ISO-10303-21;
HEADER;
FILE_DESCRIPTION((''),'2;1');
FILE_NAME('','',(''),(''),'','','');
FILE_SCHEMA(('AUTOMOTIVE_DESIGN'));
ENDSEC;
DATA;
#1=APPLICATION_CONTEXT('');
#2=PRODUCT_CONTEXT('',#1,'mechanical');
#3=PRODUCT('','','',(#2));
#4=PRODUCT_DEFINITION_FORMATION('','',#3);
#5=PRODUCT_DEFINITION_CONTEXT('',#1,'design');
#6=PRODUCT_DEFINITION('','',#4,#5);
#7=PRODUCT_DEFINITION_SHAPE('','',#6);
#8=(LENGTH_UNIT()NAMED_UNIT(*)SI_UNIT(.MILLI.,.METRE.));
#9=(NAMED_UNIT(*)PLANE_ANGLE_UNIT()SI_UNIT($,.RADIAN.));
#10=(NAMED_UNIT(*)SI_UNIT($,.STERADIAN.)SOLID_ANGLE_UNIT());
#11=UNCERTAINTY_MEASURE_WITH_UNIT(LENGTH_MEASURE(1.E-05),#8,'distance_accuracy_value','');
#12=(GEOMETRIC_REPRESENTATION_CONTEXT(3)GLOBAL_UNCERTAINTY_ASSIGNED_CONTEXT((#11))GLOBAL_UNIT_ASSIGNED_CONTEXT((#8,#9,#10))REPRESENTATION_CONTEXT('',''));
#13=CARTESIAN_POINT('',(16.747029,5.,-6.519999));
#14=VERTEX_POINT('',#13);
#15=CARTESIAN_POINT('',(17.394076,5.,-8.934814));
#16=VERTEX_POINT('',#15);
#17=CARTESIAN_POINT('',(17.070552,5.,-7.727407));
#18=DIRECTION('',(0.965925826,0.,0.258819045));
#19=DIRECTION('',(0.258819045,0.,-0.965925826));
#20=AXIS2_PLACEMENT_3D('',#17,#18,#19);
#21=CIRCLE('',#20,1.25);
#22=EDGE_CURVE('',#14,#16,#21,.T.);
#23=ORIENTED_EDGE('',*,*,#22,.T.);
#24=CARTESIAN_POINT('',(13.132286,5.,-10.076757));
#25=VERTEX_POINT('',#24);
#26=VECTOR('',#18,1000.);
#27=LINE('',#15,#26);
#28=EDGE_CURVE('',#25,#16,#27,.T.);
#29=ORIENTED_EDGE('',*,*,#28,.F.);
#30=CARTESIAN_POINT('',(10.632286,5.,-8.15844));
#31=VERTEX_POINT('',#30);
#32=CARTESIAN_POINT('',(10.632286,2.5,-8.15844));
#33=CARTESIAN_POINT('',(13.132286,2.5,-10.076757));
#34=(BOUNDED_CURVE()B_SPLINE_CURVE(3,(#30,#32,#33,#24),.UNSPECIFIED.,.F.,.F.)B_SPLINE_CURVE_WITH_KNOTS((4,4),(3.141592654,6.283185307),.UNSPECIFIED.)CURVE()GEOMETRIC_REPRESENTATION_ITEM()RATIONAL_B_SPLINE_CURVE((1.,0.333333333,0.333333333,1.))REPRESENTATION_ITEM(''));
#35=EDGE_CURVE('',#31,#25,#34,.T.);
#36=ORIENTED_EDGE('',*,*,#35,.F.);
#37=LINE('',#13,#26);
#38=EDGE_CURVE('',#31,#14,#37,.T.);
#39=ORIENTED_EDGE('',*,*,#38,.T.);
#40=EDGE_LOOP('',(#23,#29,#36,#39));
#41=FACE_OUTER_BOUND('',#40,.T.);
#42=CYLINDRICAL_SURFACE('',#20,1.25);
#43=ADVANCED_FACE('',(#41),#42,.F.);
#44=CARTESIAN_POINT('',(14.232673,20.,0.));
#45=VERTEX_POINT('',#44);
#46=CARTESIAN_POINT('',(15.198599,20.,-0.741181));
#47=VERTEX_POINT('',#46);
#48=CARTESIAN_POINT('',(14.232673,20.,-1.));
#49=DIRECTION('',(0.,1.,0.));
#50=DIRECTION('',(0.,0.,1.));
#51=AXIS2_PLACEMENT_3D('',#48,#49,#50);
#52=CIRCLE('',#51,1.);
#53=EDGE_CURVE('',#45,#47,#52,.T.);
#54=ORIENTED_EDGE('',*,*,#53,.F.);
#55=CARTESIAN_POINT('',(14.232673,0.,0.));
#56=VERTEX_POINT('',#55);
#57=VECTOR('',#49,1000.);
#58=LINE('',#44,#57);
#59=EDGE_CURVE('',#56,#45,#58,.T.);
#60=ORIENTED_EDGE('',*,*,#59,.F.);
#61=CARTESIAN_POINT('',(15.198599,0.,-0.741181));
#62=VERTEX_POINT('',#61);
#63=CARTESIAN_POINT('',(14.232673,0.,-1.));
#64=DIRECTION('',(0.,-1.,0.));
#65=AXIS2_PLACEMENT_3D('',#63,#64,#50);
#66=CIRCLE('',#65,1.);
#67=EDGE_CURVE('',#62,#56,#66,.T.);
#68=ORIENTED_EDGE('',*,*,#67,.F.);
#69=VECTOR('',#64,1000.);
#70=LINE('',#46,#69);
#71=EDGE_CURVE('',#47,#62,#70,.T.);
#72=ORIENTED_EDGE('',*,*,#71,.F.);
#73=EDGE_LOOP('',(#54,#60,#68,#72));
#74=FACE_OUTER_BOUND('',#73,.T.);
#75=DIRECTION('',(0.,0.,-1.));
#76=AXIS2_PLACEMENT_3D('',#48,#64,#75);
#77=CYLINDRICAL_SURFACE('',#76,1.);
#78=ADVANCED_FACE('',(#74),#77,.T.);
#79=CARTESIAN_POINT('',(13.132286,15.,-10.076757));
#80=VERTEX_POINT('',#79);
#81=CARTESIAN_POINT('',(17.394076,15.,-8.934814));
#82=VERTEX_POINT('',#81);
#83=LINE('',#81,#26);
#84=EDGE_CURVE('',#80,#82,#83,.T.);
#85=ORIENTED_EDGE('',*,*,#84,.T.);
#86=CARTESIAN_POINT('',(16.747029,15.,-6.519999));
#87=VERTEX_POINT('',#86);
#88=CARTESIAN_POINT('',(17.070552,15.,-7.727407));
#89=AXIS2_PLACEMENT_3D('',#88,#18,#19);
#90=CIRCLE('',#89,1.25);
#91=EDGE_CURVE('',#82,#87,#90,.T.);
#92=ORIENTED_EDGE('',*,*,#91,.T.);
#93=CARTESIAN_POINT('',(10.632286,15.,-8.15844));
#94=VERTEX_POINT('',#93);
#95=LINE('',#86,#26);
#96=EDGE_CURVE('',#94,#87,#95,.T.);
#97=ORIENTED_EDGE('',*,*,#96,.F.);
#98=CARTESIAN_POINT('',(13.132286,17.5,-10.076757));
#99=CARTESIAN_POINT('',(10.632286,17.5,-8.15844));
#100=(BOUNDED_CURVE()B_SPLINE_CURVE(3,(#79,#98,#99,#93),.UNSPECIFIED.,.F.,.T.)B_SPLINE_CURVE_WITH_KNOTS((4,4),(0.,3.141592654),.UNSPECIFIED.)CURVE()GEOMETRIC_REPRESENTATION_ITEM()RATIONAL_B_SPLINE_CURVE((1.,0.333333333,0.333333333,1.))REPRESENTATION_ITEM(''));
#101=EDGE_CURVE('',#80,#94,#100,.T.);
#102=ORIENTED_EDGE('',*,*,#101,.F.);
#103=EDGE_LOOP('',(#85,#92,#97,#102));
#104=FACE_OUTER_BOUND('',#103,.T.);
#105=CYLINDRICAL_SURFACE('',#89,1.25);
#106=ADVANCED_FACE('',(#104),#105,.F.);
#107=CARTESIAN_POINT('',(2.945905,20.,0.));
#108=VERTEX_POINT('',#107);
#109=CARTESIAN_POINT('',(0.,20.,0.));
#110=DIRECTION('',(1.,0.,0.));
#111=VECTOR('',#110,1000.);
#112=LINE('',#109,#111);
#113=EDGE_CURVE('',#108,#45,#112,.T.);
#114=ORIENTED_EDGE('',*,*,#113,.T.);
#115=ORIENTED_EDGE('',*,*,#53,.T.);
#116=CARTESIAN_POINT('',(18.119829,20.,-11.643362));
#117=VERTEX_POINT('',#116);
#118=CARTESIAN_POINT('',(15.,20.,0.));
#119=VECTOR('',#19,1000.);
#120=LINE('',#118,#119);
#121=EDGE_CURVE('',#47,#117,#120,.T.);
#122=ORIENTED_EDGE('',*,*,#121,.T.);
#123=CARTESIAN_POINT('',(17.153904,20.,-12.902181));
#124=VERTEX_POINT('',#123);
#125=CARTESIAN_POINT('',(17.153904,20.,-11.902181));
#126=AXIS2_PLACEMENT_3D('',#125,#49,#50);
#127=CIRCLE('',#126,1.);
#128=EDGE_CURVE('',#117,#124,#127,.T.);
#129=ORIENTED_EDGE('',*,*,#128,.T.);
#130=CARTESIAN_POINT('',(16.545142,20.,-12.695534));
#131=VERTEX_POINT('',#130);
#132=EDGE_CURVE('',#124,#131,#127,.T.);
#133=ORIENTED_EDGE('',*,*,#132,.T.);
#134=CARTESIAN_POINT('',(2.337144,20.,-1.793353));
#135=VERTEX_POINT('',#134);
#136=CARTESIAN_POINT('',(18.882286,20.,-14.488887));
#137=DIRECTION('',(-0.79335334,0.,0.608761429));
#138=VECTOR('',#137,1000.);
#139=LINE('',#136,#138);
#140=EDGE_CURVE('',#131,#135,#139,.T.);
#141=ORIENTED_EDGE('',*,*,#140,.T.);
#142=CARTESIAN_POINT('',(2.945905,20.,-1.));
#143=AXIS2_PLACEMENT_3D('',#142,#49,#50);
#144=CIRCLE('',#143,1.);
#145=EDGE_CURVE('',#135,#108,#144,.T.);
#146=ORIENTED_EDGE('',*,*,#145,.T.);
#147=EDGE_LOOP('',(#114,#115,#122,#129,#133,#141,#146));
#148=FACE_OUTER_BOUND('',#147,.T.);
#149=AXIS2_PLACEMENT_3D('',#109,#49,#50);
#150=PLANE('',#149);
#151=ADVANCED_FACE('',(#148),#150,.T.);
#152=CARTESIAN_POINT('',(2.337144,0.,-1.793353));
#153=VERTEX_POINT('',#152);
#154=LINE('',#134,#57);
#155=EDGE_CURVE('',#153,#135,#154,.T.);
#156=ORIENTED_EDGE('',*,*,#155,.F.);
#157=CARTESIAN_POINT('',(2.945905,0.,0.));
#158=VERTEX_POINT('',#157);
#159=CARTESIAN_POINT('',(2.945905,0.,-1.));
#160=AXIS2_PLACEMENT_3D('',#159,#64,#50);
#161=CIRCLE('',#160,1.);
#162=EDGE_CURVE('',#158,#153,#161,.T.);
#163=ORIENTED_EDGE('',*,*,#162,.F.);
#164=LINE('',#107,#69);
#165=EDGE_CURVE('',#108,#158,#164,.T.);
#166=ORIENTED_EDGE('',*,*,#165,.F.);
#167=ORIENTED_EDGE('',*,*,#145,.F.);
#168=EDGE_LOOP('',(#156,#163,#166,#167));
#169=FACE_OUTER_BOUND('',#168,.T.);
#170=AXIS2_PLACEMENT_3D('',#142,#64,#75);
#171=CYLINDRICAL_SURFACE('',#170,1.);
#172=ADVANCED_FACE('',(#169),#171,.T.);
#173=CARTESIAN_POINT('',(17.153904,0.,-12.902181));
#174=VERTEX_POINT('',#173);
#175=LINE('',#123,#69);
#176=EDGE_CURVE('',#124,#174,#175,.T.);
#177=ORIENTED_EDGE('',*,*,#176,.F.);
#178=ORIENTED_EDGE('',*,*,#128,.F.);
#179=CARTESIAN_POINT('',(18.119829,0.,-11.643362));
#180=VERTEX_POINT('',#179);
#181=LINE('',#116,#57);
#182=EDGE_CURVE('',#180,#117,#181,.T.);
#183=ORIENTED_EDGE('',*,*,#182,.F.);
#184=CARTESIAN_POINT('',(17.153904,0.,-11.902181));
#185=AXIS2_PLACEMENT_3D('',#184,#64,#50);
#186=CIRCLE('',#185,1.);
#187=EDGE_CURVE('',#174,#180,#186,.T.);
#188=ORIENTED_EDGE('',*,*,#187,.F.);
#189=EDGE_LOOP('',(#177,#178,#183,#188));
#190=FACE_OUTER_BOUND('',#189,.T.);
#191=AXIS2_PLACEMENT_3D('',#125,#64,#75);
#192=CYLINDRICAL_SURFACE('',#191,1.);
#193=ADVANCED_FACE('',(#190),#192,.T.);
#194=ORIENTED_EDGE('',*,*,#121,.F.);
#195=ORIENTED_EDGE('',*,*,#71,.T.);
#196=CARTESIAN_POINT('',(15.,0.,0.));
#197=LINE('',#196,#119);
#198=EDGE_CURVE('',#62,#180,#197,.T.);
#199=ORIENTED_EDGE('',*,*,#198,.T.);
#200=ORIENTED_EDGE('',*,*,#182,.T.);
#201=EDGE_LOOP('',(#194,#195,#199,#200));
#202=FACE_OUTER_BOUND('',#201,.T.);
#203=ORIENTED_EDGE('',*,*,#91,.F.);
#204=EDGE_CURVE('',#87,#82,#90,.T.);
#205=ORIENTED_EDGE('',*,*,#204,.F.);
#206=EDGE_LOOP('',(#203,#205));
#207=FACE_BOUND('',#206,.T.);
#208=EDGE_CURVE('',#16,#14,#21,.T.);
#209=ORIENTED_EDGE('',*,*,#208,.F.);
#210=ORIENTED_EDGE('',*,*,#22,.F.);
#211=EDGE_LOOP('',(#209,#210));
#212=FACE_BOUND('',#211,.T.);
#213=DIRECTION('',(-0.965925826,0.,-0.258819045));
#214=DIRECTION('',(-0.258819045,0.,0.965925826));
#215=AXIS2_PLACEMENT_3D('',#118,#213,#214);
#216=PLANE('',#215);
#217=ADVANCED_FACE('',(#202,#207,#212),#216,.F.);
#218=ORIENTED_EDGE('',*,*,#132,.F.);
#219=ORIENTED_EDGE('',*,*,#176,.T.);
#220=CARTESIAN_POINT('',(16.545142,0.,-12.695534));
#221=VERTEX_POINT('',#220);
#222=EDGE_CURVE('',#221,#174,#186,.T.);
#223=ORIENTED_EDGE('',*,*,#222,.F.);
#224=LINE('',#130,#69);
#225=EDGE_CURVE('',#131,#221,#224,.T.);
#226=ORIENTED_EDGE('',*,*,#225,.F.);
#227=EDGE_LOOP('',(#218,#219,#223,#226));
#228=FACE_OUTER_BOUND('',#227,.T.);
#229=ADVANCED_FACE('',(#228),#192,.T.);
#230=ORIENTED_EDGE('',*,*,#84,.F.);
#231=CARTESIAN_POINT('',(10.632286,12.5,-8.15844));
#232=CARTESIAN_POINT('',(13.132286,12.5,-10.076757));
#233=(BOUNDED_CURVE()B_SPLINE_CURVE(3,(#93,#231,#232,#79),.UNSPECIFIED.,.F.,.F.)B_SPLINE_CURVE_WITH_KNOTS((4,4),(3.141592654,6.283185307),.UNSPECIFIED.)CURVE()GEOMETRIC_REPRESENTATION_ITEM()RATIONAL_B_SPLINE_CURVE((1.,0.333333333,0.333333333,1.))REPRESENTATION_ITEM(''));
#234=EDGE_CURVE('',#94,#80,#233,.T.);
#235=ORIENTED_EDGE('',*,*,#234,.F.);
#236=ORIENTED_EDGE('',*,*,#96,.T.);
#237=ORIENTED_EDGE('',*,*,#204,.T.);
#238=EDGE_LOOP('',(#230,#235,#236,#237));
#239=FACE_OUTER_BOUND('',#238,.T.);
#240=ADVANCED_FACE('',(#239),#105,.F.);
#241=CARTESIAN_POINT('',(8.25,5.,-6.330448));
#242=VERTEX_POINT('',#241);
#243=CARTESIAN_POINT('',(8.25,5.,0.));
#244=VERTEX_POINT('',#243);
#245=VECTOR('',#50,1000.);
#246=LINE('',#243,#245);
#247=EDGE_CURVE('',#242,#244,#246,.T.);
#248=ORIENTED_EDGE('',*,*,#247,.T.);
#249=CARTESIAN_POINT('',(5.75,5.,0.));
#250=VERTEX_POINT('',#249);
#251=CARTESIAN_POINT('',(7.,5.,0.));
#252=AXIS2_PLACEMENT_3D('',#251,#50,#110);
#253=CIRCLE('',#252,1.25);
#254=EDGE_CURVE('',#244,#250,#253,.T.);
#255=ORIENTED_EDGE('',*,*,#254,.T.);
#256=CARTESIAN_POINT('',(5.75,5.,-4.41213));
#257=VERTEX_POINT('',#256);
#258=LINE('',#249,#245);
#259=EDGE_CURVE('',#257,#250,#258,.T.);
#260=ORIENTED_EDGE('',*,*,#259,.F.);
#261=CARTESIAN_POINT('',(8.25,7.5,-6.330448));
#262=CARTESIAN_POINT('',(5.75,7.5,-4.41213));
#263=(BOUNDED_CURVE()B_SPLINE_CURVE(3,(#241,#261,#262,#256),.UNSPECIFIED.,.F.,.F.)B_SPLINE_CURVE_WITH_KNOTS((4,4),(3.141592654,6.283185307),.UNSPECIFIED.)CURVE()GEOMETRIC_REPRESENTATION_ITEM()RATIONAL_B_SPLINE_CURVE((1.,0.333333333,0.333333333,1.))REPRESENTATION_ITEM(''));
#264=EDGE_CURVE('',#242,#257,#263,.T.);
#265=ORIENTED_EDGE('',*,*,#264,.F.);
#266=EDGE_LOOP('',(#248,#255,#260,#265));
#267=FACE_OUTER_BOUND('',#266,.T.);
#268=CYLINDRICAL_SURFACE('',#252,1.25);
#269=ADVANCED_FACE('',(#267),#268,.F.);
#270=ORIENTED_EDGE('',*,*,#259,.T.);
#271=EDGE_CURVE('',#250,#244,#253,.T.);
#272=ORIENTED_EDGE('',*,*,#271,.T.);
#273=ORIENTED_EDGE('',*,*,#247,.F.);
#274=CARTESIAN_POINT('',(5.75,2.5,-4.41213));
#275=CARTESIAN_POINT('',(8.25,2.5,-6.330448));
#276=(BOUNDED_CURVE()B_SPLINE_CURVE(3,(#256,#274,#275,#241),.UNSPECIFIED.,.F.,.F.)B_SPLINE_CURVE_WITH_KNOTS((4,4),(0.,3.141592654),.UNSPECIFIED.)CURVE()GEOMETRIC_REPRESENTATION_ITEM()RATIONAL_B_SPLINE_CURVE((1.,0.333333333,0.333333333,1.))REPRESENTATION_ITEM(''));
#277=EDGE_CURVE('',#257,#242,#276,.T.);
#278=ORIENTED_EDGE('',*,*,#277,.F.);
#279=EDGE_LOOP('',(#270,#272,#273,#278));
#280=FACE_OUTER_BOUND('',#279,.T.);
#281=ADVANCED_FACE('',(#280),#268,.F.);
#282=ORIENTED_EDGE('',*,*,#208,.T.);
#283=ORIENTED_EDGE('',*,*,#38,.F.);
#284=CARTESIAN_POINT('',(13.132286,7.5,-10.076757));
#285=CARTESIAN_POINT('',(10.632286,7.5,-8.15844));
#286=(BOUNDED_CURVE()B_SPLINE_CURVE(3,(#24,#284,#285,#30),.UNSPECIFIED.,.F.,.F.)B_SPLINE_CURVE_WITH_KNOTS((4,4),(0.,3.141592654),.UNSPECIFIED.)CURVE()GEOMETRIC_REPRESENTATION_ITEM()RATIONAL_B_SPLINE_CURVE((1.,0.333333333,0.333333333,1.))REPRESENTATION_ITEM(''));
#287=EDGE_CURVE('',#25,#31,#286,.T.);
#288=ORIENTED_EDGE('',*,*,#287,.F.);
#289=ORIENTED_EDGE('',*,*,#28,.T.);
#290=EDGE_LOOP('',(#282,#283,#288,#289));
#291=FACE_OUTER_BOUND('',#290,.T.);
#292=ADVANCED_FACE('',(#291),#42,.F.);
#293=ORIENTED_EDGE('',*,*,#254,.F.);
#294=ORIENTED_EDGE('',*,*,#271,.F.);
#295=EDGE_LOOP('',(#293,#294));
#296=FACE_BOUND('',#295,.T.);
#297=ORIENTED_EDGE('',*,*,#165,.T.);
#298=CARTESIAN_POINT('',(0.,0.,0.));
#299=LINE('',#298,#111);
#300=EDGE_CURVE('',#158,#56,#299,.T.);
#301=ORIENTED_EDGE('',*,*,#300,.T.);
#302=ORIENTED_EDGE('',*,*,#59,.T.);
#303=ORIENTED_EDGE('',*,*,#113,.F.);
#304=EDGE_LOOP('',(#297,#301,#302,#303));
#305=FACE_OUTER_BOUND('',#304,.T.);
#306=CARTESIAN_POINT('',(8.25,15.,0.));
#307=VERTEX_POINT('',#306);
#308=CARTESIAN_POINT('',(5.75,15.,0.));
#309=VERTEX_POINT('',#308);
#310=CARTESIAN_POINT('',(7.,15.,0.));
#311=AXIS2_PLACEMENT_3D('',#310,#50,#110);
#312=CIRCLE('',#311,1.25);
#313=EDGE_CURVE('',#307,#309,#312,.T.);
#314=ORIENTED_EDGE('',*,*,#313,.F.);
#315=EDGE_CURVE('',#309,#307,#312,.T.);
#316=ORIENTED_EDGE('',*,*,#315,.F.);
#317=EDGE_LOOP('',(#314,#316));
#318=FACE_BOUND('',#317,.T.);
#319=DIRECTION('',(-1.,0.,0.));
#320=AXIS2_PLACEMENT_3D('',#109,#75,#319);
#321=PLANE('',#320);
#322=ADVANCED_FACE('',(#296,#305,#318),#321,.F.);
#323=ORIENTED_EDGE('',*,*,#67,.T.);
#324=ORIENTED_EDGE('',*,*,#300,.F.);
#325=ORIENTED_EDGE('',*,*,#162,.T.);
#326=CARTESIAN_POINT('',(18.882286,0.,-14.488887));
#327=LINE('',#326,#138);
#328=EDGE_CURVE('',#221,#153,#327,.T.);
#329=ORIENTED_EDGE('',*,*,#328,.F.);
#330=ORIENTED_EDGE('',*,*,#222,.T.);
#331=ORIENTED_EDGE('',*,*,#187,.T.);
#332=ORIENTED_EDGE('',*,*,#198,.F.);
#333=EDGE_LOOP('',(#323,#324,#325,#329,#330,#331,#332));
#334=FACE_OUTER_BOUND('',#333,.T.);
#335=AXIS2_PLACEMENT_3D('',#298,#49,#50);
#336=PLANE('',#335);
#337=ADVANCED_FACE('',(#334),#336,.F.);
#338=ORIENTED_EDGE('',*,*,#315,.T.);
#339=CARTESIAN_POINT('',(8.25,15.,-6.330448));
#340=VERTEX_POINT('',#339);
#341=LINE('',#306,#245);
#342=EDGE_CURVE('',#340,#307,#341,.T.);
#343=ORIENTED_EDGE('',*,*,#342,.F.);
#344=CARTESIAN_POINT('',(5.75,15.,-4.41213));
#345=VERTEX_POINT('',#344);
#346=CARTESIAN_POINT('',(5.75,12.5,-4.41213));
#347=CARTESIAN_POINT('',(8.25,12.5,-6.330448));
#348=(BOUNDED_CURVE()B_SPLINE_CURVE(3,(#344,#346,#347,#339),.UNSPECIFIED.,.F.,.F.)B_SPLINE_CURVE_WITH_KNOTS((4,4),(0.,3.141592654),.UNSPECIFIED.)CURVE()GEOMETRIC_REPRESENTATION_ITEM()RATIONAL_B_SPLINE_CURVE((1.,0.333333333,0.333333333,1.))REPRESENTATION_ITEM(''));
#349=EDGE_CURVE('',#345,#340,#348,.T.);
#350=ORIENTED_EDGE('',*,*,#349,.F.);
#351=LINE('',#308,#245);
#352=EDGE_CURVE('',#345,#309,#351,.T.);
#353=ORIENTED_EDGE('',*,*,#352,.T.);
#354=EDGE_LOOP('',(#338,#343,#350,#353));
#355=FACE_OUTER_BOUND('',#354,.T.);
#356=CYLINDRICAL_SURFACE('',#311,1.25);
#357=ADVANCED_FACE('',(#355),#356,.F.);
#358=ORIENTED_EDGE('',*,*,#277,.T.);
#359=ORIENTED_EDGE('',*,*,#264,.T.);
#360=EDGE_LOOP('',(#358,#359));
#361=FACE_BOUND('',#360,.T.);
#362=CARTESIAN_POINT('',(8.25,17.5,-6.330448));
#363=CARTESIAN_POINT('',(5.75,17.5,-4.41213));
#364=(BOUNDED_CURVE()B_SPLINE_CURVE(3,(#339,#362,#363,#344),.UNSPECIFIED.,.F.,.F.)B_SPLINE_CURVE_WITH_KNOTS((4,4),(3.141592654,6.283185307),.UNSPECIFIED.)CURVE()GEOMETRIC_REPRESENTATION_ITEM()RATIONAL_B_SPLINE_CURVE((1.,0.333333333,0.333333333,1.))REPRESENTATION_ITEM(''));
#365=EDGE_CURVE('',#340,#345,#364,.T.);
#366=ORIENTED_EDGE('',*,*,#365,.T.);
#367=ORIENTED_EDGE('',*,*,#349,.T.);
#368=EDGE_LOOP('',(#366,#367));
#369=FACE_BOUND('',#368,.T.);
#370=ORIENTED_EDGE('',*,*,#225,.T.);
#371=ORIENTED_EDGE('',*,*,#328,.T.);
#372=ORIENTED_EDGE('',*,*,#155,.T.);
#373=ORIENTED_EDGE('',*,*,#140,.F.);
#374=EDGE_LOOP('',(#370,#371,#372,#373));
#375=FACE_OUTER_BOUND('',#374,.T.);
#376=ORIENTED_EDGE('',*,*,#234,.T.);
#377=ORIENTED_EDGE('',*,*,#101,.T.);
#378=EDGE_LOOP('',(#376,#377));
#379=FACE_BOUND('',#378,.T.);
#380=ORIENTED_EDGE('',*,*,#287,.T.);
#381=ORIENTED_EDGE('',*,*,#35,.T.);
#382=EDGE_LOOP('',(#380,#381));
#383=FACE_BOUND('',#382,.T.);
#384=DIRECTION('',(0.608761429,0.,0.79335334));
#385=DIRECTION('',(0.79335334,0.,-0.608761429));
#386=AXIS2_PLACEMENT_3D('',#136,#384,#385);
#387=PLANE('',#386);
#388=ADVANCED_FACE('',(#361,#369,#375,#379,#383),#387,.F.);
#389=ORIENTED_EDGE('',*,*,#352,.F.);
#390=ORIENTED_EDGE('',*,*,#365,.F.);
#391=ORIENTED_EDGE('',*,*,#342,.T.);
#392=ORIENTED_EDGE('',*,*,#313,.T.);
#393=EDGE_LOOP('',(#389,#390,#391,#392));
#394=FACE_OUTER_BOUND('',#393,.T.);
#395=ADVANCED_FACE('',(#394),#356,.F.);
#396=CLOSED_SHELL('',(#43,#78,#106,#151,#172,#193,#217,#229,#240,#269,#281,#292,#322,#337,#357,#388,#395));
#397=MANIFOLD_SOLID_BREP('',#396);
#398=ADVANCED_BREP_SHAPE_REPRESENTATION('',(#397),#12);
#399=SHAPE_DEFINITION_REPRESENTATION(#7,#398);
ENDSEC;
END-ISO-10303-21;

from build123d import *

# Parameters (mm, degrees)
EXTRUDE_1_DEPTH             = 20
HOLE_WIZARD_M3_1_AT_2_COUNT = 2
HOLE_WIZARD_M3_1_AT_2_PITCH = 10
FILLET_1_R                  = 1


with BuildPart() as part:
    # 草图1 → 凸台-拉伸1 (new body)
    with BuildSketch(Plane(origin=(0, 0, 0), x_dir=(1, 0, 0), z_dir=(0, 1, 0))):
        Polygon((0, 0), (15, 0), (18.882285677, 14.488887394), align=None)
    extrude(amount=EXTRUDE_1_DEPTH)

    # 草图4 → M3 螺纹孔1 (revolve, cut)
    with BuildSketch(Plane(origin=(17.070552361, 15, -7.72740661), x_dir=(0.25881904510251796, 0, -0.9659258262890691), z_dir=(0, 1, 0))):
        Polygon((0, 0), (0, 7.5), (1.25, 6.748924226), (1.25, 0), align=None)
    hole_wizard_m3_1 = revolve(axis=Axis((23.204181358, 15, -6.083905674), (-0.9659258262890691, 0, -0.2588190451025179)), mode=Mode.SUBTRACT)

    # M3 螺纹孔1 at 2: M3 螺纹孔1 ×2
    with Locations(*[(0, -i * HOLE_WIZARD_M3_1_AT_2_PITCH, 0) for i in range(1, HOLE_WIZARD_M3_1_AT_2_COUNT)]):
        add(hole_wizard_m3_1, mode=Mode.SUBTRACT)

    # 镜向1: M3 螺纹孔1 across plane
    add(hole_wizard_m3_1.mirror(Plane(origin=(9.441142838, 0, -7.244443697), x_dir=(0.6087614290087218, 0, 0.7933533402912344), z_dir=(0.7933533402912343, 0, -0.6087614290087218))), mode=Mode.SUBTRACT)

    # 镜向1 copy 1 sketch → 镜向1 copy 1 (revolve, cut)
    with BuildSketch(Plane(origin=(7, 5, 0), x_dir=(-1, 0, 0), z_dir=(0, 1, 0))):
        Polygon((0, 0), (0, -7.5), (1.25, -6.748924226), (1.25, 0), align=None)
    revolve(axis=Axis((7, 5, 6.35), (0, 0, 1)), mode=Mode.SUBTRACT)

    # 圆角1
    fillet_1_edges = [part.edges().sort_by_distance(p)[0] for p in [
        (18.882285677, 10, -14.488887394),
        (15, 10, 0),
        (0, 10, 0),
    ]]
    fillet(fillet_1_edges, radius=FILLET_1_R)


solid = part.part
